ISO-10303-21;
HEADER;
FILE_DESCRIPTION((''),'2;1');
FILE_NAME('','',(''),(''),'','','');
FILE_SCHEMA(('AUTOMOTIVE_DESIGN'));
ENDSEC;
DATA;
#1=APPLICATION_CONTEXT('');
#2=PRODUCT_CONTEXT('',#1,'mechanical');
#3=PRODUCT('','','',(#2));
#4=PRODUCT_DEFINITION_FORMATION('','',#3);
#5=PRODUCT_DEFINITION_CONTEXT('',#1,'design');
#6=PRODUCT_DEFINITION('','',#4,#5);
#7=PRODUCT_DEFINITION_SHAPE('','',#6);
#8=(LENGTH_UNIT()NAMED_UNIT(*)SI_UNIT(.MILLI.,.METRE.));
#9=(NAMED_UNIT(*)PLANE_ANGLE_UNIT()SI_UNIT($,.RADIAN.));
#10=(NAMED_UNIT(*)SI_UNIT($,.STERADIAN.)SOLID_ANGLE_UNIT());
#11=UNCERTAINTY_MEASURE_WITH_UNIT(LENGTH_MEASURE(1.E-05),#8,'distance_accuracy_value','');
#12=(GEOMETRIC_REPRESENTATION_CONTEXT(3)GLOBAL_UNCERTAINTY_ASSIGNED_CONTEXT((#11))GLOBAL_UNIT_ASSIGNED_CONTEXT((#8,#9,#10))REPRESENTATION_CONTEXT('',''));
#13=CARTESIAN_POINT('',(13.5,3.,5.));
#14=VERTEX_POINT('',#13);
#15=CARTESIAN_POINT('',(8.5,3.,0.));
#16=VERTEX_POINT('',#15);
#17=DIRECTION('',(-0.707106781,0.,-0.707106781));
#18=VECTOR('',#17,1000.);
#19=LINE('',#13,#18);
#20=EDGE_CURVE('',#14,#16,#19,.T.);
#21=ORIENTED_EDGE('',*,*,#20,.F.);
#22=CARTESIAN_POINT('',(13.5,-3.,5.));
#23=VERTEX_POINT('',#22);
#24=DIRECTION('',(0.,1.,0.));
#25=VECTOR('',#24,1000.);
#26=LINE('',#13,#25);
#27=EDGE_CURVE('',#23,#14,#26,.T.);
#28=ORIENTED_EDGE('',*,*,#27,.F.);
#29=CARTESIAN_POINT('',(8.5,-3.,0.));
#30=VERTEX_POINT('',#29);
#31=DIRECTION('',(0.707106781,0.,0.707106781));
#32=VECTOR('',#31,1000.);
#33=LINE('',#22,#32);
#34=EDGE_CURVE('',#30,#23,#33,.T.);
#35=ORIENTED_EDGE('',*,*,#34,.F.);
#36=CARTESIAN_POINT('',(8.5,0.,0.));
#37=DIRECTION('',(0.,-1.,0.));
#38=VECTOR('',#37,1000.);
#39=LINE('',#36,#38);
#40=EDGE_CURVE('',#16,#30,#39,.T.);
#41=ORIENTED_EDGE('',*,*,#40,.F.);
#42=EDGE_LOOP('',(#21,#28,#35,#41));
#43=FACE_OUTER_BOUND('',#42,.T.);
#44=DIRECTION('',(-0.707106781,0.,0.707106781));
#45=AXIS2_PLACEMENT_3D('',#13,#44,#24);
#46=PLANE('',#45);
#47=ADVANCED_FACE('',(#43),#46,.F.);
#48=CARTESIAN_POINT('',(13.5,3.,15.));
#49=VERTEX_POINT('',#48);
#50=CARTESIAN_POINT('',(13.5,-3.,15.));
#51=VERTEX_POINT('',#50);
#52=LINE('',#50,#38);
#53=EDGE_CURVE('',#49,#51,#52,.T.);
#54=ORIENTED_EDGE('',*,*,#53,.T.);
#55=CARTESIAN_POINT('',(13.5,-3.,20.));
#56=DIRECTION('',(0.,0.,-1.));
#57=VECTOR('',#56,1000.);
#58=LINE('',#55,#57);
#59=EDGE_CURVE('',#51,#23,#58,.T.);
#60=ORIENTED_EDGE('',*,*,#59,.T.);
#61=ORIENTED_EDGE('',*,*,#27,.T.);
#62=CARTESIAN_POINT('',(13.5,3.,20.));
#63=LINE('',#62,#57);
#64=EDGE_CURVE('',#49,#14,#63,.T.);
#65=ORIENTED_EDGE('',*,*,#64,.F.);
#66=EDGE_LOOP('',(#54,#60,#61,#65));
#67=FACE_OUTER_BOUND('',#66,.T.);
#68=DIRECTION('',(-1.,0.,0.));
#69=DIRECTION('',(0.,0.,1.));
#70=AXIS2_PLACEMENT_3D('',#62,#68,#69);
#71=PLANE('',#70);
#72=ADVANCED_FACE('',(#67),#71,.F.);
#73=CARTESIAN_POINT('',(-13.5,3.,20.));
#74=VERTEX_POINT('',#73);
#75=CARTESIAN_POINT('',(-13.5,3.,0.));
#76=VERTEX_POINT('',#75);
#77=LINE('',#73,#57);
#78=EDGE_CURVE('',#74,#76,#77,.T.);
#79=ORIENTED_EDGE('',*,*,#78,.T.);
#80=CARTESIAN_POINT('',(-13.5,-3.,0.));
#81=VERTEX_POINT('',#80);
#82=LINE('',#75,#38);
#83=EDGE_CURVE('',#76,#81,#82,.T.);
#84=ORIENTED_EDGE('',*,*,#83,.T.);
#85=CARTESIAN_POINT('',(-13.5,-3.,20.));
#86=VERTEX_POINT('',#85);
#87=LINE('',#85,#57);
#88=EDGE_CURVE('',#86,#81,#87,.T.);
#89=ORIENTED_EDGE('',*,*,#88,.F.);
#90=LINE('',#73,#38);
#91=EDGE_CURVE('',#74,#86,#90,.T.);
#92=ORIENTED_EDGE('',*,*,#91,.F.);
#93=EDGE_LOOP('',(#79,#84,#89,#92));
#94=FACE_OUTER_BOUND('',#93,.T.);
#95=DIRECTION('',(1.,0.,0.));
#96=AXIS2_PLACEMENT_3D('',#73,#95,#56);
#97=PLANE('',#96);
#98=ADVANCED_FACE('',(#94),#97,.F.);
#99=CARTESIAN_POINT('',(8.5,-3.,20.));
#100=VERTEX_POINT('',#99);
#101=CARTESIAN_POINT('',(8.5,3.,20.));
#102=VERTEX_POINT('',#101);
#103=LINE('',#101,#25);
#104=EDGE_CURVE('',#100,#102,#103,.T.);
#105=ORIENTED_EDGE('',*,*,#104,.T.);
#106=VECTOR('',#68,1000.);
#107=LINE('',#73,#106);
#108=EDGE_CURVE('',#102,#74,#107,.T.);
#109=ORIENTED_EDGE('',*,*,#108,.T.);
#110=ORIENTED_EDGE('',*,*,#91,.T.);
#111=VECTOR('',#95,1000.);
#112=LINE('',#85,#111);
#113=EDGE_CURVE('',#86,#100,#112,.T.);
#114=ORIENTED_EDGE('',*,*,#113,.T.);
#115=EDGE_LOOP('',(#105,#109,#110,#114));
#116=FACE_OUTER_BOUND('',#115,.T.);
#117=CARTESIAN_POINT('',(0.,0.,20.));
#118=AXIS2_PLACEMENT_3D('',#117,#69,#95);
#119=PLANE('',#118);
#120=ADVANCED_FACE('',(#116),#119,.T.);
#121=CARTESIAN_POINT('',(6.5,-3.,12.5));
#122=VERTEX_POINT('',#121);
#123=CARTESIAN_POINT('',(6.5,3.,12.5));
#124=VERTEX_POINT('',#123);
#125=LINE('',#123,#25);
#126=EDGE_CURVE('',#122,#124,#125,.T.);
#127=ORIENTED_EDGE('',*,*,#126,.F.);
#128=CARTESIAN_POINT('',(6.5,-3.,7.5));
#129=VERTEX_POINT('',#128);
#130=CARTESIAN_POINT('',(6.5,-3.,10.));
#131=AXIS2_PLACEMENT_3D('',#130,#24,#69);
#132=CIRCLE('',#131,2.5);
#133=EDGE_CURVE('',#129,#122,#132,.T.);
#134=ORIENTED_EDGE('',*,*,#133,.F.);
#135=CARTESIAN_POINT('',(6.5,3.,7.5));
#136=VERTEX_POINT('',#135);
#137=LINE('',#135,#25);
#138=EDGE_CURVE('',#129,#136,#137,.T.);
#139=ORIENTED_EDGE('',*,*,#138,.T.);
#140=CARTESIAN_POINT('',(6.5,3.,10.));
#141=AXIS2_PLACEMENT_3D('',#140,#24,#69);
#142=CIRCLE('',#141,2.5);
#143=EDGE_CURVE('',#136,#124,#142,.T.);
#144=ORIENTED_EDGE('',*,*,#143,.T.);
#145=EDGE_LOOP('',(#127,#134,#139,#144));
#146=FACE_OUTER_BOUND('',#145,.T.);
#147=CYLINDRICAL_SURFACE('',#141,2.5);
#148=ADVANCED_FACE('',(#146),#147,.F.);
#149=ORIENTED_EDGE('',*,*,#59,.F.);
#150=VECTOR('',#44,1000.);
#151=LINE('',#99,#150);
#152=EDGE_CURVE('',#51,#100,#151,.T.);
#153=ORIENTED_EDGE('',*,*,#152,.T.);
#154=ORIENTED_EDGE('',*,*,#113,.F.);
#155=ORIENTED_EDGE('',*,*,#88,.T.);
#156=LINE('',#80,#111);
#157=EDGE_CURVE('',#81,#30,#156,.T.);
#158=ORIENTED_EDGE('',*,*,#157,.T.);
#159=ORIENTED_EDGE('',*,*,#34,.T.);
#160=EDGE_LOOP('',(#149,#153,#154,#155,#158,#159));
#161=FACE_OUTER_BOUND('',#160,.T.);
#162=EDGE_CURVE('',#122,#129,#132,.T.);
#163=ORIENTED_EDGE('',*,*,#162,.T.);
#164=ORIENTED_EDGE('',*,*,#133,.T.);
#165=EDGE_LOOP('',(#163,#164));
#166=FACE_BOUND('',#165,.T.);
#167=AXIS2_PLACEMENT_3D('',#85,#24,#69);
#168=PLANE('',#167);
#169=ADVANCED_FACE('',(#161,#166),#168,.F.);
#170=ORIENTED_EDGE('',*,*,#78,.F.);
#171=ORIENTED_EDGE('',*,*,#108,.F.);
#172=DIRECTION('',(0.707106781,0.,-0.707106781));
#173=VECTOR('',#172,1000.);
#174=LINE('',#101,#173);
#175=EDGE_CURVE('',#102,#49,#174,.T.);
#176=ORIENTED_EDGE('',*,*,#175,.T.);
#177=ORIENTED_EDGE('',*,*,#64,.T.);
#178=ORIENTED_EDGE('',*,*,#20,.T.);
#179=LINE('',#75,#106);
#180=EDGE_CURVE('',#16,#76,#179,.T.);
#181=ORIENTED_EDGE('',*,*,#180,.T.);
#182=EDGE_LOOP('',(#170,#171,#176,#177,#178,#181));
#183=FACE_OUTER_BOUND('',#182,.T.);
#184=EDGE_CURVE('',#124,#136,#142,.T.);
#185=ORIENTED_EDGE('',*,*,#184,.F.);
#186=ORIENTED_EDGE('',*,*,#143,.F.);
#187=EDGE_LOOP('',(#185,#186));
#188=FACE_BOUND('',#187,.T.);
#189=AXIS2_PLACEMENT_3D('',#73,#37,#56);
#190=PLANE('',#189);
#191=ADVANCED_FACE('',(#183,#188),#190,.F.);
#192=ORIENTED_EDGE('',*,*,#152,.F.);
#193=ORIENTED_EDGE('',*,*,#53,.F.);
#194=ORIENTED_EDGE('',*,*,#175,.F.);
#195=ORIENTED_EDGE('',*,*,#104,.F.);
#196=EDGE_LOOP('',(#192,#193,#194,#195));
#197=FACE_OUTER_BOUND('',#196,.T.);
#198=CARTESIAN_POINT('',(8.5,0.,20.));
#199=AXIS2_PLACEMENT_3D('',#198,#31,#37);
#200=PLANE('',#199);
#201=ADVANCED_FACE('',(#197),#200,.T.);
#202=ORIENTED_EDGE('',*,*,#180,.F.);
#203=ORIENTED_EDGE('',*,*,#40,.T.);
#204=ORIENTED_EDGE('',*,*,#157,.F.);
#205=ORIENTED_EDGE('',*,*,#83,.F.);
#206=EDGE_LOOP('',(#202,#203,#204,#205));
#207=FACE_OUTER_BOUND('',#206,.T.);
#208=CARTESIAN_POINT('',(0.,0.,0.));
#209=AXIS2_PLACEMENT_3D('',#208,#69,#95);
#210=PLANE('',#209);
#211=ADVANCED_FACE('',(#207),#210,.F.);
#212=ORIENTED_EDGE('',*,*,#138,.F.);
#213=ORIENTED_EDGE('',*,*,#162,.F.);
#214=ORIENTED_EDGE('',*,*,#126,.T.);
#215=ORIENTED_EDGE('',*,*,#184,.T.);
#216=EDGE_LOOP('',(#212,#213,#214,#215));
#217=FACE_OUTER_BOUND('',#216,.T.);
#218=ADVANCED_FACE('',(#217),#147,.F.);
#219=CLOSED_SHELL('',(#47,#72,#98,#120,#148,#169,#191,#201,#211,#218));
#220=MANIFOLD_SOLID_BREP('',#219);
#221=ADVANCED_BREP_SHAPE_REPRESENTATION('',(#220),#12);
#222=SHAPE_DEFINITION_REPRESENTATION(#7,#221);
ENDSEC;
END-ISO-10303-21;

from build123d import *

# Parameters (mm, degrees)
SKETCH_1_W             = 27
SKETCH_1_H             = 6
EXTRUDE_1_DEPTH        = 20
HOLE_WIZARD_M6_1_D     = 5
HOLE_WIZARD_M6_1_DEPTH = 15
HOLE_WIZARD_M6_1_TIP   = 1.502151548
CHAMFER_1_SIZE         = 5


with BuildPart() as part:
    # 草图1 → 凸台-拉伸1 (new body)
    with BuildSketch(Plane.XY):
        Rectangle(SKETCH_1_W, SKETCH_1_H)
    extrude(amount=EXTRUDE_1_DEPTH)

    # M6 螺纹孔1
    with Locations(Plane(origin=(0, 3, 0), x_dir=(1, 0, 0), z_dir=(0, 1, 0))):
        with Locations((6.5, -10)):
            Hole(HOLE_WIZARD_M6_1_D / 2, depth=HOLE_WIZARD_M6_1_DEPTH)
            with Locations((0, 0, -(HOLE_WIZARD_M6_1_DEPTH + HOLE_WIZARD_M6_1_TIP / 2))):  # 118° drill point
                Cone(0, HOLE_WIZARD_M6_1_D / 2, HOLE_WIZARD_M6_1_TIP, mode=Mode.SUBTRACT)

    # 倒角1
    chamfer_1_edges = [part.edges().sort_by_distance(p)[0] for p in [
        (13.5, 0, 20),
        (13.5, 0, 0),
    ]]
    chamfer(chamfer_1_edges, length=CHAMFER_1_SIZE)


solid = part.part
